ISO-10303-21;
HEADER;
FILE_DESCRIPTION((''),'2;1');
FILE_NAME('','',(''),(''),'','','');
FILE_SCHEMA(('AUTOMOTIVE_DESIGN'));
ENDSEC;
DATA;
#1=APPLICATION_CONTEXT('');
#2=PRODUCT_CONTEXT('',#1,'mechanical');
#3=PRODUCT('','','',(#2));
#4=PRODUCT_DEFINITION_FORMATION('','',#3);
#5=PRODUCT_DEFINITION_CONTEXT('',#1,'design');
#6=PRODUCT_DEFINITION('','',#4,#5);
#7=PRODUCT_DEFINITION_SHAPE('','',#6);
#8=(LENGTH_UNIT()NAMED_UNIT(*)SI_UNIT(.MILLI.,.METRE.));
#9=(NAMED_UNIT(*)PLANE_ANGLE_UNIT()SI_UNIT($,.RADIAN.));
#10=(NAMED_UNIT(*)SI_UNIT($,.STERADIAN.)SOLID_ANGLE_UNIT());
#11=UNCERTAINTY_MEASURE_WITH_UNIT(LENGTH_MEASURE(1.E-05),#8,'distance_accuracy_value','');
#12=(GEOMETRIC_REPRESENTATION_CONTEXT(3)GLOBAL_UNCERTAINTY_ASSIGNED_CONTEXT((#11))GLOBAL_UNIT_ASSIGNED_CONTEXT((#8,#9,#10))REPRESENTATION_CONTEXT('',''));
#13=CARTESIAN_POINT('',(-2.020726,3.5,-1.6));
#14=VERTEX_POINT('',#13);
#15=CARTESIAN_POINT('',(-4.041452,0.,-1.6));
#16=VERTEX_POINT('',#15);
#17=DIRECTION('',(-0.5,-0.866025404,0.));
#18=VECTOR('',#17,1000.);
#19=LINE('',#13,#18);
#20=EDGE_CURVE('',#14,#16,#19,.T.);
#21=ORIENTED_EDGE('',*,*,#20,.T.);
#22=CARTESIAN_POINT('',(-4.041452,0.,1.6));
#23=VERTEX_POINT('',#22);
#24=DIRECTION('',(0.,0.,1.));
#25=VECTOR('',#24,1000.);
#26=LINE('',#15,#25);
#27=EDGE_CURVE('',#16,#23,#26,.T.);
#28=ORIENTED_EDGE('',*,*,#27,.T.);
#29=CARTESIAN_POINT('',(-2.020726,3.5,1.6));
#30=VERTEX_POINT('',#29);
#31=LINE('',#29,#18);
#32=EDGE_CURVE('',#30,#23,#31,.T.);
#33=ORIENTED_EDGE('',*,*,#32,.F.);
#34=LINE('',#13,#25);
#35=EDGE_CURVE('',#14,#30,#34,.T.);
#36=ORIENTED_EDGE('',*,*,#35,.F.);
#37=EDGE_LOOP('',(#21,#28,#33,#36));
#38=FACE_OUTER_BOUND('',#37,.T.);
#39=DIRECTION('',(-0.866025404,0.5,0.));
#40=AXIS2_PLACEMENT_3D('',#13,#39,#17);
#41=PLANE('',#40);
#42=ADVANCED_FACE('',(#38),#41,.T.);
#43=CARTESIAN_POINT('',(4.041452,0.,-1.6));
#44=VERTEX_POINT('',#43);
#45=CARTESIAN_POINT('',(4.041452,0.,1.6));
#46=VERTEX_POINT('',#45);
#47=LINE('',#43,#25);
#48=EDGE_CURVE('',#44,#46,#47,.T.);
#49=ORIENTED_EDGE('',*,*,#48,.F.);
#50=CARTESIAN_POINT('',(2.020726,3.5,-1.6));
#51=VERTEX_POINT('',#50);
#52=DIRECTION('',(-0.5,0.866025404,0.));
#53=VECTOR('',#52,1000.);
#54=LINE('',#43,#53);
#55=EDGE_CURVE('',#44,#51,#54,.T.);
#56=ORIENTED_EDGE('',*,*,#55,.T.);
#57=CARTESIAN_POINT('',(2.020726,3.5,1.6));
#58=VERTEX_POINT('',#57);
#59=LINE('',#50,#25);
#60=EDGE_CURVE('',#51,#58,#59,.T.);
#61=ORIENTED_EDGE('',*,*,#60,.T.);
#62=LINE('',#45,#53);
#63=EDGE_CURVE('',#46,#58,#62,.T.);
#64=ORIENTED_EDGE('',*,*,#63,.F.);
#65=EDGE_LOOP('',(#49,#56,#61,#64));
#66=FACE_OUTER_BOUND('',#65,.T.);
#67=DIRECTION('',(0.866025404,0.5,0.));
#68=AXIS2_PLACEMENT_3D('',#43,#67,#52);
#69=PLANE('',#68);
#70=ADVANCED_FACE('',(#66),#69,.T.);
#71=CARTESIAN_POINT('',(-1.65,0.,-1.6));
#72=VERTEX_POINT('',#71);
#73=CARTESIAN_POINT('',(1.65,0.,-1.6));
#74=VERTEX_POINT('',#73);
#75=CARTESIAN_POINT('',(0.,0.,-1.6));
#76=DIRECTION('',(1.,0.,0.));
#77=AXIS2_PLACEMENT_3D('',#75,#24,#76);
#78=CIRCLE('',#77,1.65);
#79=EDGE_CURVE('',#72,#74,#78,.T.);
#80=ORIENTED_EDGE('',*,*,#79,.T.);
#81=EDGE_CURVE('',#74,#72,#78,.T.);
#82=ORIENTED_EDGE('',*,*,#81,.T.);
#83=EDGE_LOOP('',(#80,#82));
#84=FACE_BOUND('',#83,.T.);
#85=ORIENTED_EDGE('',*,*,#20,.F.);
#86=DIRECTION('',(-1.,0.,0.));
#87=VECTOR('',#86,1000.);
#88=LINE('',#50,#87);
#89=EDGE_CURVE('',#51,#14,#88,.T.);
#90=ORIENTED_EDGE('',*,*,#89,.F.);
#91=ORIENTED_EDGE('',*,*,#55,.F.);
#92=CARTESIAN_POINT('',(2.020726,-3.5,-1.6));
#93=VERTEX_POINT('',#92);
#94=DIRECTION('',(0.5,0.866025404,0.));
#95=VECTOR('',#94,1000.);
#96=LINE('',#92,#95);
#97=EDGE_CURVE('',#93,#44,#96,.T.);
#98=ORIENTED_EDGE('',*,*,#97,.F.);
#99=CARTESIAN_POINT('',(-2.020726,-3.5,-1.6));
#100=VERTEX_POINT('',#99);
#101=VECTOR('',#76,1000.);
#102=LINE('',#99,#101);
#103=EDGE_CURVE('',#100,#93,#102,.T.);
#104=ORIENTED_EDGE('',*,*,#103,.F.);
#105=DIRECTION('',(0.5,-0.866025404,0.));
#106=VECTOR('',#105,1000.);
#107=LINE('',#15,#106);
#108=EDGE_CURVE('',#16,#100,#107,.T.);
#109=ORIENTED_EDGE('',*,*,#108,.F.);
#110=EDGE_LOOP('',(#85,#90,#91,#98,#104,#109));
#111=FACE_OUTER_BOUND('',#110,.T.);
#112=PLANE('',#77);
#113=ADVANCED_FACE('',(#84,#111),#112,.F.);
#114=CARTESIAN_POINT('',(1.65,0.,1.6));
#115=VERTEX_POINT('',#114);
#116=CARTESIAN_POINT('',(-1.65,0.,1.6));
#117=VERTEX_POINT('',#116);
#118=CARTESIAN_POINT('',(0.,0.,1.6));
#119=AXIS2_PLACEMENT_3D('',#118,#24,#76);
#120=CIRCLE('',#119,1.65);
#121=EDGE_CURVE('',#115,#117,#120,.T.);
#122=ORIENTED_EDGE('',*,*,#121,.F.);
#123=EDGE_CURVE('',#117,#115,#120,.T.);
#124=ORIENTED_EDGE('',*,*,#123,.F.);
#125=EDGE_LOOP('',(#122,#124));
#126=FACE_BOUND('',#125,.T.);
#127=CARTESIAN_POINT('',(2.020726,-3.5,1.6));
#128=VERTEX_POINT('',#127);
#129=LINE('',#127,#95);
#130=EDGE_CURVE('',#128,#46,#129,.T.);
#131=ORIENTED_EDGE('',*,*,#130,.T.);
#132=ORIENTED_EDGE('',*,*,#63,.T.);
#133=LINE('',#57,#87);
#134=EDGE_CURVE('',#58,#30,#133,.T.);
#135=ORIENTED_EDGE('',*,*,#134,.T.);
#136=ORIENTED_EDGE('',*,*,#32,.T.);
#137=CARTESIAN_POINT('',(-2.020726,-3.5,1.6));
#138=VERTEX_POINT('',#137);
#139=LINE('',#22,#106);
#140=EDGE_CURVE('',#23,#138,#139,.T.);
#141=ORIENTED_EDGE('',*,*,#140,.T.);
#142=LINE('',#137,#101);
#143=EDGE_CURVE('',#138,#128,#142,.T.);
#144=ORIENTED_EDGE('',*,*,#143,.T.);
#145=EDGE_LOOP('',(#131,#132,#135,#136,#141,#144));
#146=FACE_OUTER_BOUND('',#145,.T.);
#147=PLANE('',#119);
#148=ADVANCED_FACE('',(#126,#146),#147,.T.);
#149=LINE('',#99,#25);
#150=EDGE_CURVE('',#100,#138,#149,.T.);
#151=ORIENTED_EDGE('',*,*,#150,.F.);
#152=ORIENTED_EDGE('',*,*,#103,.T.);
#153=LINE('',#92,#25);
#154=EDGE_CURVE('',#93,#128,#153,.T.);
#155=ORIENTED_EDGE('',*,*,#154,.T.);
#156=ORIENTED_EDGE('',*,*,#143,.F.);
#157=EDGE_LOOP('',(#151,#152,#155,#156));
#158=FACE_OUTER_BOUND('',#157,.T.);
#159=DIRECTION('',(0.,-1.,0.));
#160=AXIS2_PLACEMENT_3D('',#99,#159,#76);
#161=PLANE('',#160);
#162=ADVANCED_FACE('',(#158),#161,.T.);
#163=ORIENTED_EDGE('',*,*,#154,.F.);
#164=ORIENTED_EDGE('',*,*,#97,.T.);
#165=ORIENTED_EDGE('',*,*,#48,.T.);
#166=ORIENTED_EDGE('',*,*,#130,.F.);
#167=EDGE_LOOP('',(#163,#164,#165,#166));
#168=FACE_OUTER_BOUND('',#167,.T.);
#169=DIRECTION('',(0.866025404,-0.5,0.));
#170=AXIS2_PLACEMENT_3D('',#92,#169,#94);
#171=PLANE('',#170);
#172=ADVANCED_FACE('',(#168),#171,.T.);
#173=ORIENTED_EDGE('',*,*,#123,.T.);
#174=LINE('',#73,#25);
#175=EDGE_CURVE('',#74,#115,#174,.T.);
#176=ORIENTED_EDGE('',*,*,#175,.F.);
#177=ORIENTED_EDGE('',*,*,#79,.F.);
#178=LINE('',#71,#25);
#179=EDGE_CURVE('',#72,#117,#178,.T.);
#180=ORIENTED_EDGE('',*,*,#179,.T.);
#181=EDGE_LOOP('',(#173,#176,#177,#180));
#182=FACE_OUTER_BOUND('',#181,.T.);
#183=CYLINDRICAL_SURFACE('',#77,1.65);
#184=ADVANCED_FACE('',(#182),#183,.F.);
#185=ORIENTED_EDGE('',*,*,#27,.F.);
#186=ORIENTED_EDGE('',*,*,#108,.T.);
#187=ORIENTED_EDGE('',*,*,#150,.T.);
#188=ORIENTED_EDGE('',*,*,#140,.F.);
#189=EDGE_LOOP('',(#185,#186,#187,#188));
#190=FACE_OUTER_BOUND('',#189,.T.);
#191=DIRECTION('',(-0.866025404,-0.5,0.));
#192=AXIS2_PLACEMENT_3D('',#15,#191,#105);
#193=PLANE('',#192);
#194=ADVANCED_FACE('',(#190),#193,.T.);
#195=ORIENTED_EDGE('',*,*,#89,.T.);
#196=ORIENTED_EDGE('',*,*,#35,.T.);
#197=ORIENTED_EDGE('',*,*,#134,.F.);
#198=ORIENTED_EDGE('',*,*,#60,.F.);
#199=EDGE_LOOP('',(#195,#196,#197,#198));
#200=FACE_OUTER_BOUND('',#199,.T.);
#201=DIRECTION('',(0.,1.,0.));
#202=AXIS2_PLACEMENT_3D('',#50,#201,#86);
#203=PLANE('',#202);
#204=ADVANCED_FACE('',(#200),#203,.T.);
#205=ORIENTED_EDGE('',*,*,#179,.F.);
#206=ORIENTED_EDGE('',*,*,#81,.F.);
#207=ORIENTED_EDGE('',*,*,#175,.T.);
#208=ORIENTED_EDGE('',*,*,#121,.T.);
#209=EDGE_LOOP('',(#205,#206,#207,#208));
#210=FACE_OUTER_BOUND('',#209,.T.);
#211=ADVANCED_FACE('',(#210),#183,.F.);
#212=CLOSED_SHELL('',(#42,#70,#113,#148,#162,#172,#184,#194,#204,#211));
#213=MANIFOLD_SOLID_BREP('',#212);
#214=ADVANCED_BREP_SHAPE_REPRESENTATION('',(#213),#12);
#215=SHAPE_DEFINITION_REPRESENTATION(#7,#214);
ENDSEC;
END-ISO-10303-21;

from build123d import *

# Parameters (mm, degrees)
SKETCH_1_R      = 1.65
EXTRUDE_1_DEPTH = 1.6


with BuildPart() as part:
    # 草图1 → 凸台-拉伸1 (new, symmetric)
    with BuildSketch(Plane.XY):
        Polygon((4.041451884, 0), (2.020725942, 3.5), (-2.020725942, 3.5), (-4.041451884, 0), (-2.020725942, -3.5), (2.020725942, -3.5), align=None)
        Circle(SKETCH_1_R, mode=Mode.SUBTRACT)
    extrude(amount=EXTRUDE_1_DEPTH, both=True)


solid = part.part
